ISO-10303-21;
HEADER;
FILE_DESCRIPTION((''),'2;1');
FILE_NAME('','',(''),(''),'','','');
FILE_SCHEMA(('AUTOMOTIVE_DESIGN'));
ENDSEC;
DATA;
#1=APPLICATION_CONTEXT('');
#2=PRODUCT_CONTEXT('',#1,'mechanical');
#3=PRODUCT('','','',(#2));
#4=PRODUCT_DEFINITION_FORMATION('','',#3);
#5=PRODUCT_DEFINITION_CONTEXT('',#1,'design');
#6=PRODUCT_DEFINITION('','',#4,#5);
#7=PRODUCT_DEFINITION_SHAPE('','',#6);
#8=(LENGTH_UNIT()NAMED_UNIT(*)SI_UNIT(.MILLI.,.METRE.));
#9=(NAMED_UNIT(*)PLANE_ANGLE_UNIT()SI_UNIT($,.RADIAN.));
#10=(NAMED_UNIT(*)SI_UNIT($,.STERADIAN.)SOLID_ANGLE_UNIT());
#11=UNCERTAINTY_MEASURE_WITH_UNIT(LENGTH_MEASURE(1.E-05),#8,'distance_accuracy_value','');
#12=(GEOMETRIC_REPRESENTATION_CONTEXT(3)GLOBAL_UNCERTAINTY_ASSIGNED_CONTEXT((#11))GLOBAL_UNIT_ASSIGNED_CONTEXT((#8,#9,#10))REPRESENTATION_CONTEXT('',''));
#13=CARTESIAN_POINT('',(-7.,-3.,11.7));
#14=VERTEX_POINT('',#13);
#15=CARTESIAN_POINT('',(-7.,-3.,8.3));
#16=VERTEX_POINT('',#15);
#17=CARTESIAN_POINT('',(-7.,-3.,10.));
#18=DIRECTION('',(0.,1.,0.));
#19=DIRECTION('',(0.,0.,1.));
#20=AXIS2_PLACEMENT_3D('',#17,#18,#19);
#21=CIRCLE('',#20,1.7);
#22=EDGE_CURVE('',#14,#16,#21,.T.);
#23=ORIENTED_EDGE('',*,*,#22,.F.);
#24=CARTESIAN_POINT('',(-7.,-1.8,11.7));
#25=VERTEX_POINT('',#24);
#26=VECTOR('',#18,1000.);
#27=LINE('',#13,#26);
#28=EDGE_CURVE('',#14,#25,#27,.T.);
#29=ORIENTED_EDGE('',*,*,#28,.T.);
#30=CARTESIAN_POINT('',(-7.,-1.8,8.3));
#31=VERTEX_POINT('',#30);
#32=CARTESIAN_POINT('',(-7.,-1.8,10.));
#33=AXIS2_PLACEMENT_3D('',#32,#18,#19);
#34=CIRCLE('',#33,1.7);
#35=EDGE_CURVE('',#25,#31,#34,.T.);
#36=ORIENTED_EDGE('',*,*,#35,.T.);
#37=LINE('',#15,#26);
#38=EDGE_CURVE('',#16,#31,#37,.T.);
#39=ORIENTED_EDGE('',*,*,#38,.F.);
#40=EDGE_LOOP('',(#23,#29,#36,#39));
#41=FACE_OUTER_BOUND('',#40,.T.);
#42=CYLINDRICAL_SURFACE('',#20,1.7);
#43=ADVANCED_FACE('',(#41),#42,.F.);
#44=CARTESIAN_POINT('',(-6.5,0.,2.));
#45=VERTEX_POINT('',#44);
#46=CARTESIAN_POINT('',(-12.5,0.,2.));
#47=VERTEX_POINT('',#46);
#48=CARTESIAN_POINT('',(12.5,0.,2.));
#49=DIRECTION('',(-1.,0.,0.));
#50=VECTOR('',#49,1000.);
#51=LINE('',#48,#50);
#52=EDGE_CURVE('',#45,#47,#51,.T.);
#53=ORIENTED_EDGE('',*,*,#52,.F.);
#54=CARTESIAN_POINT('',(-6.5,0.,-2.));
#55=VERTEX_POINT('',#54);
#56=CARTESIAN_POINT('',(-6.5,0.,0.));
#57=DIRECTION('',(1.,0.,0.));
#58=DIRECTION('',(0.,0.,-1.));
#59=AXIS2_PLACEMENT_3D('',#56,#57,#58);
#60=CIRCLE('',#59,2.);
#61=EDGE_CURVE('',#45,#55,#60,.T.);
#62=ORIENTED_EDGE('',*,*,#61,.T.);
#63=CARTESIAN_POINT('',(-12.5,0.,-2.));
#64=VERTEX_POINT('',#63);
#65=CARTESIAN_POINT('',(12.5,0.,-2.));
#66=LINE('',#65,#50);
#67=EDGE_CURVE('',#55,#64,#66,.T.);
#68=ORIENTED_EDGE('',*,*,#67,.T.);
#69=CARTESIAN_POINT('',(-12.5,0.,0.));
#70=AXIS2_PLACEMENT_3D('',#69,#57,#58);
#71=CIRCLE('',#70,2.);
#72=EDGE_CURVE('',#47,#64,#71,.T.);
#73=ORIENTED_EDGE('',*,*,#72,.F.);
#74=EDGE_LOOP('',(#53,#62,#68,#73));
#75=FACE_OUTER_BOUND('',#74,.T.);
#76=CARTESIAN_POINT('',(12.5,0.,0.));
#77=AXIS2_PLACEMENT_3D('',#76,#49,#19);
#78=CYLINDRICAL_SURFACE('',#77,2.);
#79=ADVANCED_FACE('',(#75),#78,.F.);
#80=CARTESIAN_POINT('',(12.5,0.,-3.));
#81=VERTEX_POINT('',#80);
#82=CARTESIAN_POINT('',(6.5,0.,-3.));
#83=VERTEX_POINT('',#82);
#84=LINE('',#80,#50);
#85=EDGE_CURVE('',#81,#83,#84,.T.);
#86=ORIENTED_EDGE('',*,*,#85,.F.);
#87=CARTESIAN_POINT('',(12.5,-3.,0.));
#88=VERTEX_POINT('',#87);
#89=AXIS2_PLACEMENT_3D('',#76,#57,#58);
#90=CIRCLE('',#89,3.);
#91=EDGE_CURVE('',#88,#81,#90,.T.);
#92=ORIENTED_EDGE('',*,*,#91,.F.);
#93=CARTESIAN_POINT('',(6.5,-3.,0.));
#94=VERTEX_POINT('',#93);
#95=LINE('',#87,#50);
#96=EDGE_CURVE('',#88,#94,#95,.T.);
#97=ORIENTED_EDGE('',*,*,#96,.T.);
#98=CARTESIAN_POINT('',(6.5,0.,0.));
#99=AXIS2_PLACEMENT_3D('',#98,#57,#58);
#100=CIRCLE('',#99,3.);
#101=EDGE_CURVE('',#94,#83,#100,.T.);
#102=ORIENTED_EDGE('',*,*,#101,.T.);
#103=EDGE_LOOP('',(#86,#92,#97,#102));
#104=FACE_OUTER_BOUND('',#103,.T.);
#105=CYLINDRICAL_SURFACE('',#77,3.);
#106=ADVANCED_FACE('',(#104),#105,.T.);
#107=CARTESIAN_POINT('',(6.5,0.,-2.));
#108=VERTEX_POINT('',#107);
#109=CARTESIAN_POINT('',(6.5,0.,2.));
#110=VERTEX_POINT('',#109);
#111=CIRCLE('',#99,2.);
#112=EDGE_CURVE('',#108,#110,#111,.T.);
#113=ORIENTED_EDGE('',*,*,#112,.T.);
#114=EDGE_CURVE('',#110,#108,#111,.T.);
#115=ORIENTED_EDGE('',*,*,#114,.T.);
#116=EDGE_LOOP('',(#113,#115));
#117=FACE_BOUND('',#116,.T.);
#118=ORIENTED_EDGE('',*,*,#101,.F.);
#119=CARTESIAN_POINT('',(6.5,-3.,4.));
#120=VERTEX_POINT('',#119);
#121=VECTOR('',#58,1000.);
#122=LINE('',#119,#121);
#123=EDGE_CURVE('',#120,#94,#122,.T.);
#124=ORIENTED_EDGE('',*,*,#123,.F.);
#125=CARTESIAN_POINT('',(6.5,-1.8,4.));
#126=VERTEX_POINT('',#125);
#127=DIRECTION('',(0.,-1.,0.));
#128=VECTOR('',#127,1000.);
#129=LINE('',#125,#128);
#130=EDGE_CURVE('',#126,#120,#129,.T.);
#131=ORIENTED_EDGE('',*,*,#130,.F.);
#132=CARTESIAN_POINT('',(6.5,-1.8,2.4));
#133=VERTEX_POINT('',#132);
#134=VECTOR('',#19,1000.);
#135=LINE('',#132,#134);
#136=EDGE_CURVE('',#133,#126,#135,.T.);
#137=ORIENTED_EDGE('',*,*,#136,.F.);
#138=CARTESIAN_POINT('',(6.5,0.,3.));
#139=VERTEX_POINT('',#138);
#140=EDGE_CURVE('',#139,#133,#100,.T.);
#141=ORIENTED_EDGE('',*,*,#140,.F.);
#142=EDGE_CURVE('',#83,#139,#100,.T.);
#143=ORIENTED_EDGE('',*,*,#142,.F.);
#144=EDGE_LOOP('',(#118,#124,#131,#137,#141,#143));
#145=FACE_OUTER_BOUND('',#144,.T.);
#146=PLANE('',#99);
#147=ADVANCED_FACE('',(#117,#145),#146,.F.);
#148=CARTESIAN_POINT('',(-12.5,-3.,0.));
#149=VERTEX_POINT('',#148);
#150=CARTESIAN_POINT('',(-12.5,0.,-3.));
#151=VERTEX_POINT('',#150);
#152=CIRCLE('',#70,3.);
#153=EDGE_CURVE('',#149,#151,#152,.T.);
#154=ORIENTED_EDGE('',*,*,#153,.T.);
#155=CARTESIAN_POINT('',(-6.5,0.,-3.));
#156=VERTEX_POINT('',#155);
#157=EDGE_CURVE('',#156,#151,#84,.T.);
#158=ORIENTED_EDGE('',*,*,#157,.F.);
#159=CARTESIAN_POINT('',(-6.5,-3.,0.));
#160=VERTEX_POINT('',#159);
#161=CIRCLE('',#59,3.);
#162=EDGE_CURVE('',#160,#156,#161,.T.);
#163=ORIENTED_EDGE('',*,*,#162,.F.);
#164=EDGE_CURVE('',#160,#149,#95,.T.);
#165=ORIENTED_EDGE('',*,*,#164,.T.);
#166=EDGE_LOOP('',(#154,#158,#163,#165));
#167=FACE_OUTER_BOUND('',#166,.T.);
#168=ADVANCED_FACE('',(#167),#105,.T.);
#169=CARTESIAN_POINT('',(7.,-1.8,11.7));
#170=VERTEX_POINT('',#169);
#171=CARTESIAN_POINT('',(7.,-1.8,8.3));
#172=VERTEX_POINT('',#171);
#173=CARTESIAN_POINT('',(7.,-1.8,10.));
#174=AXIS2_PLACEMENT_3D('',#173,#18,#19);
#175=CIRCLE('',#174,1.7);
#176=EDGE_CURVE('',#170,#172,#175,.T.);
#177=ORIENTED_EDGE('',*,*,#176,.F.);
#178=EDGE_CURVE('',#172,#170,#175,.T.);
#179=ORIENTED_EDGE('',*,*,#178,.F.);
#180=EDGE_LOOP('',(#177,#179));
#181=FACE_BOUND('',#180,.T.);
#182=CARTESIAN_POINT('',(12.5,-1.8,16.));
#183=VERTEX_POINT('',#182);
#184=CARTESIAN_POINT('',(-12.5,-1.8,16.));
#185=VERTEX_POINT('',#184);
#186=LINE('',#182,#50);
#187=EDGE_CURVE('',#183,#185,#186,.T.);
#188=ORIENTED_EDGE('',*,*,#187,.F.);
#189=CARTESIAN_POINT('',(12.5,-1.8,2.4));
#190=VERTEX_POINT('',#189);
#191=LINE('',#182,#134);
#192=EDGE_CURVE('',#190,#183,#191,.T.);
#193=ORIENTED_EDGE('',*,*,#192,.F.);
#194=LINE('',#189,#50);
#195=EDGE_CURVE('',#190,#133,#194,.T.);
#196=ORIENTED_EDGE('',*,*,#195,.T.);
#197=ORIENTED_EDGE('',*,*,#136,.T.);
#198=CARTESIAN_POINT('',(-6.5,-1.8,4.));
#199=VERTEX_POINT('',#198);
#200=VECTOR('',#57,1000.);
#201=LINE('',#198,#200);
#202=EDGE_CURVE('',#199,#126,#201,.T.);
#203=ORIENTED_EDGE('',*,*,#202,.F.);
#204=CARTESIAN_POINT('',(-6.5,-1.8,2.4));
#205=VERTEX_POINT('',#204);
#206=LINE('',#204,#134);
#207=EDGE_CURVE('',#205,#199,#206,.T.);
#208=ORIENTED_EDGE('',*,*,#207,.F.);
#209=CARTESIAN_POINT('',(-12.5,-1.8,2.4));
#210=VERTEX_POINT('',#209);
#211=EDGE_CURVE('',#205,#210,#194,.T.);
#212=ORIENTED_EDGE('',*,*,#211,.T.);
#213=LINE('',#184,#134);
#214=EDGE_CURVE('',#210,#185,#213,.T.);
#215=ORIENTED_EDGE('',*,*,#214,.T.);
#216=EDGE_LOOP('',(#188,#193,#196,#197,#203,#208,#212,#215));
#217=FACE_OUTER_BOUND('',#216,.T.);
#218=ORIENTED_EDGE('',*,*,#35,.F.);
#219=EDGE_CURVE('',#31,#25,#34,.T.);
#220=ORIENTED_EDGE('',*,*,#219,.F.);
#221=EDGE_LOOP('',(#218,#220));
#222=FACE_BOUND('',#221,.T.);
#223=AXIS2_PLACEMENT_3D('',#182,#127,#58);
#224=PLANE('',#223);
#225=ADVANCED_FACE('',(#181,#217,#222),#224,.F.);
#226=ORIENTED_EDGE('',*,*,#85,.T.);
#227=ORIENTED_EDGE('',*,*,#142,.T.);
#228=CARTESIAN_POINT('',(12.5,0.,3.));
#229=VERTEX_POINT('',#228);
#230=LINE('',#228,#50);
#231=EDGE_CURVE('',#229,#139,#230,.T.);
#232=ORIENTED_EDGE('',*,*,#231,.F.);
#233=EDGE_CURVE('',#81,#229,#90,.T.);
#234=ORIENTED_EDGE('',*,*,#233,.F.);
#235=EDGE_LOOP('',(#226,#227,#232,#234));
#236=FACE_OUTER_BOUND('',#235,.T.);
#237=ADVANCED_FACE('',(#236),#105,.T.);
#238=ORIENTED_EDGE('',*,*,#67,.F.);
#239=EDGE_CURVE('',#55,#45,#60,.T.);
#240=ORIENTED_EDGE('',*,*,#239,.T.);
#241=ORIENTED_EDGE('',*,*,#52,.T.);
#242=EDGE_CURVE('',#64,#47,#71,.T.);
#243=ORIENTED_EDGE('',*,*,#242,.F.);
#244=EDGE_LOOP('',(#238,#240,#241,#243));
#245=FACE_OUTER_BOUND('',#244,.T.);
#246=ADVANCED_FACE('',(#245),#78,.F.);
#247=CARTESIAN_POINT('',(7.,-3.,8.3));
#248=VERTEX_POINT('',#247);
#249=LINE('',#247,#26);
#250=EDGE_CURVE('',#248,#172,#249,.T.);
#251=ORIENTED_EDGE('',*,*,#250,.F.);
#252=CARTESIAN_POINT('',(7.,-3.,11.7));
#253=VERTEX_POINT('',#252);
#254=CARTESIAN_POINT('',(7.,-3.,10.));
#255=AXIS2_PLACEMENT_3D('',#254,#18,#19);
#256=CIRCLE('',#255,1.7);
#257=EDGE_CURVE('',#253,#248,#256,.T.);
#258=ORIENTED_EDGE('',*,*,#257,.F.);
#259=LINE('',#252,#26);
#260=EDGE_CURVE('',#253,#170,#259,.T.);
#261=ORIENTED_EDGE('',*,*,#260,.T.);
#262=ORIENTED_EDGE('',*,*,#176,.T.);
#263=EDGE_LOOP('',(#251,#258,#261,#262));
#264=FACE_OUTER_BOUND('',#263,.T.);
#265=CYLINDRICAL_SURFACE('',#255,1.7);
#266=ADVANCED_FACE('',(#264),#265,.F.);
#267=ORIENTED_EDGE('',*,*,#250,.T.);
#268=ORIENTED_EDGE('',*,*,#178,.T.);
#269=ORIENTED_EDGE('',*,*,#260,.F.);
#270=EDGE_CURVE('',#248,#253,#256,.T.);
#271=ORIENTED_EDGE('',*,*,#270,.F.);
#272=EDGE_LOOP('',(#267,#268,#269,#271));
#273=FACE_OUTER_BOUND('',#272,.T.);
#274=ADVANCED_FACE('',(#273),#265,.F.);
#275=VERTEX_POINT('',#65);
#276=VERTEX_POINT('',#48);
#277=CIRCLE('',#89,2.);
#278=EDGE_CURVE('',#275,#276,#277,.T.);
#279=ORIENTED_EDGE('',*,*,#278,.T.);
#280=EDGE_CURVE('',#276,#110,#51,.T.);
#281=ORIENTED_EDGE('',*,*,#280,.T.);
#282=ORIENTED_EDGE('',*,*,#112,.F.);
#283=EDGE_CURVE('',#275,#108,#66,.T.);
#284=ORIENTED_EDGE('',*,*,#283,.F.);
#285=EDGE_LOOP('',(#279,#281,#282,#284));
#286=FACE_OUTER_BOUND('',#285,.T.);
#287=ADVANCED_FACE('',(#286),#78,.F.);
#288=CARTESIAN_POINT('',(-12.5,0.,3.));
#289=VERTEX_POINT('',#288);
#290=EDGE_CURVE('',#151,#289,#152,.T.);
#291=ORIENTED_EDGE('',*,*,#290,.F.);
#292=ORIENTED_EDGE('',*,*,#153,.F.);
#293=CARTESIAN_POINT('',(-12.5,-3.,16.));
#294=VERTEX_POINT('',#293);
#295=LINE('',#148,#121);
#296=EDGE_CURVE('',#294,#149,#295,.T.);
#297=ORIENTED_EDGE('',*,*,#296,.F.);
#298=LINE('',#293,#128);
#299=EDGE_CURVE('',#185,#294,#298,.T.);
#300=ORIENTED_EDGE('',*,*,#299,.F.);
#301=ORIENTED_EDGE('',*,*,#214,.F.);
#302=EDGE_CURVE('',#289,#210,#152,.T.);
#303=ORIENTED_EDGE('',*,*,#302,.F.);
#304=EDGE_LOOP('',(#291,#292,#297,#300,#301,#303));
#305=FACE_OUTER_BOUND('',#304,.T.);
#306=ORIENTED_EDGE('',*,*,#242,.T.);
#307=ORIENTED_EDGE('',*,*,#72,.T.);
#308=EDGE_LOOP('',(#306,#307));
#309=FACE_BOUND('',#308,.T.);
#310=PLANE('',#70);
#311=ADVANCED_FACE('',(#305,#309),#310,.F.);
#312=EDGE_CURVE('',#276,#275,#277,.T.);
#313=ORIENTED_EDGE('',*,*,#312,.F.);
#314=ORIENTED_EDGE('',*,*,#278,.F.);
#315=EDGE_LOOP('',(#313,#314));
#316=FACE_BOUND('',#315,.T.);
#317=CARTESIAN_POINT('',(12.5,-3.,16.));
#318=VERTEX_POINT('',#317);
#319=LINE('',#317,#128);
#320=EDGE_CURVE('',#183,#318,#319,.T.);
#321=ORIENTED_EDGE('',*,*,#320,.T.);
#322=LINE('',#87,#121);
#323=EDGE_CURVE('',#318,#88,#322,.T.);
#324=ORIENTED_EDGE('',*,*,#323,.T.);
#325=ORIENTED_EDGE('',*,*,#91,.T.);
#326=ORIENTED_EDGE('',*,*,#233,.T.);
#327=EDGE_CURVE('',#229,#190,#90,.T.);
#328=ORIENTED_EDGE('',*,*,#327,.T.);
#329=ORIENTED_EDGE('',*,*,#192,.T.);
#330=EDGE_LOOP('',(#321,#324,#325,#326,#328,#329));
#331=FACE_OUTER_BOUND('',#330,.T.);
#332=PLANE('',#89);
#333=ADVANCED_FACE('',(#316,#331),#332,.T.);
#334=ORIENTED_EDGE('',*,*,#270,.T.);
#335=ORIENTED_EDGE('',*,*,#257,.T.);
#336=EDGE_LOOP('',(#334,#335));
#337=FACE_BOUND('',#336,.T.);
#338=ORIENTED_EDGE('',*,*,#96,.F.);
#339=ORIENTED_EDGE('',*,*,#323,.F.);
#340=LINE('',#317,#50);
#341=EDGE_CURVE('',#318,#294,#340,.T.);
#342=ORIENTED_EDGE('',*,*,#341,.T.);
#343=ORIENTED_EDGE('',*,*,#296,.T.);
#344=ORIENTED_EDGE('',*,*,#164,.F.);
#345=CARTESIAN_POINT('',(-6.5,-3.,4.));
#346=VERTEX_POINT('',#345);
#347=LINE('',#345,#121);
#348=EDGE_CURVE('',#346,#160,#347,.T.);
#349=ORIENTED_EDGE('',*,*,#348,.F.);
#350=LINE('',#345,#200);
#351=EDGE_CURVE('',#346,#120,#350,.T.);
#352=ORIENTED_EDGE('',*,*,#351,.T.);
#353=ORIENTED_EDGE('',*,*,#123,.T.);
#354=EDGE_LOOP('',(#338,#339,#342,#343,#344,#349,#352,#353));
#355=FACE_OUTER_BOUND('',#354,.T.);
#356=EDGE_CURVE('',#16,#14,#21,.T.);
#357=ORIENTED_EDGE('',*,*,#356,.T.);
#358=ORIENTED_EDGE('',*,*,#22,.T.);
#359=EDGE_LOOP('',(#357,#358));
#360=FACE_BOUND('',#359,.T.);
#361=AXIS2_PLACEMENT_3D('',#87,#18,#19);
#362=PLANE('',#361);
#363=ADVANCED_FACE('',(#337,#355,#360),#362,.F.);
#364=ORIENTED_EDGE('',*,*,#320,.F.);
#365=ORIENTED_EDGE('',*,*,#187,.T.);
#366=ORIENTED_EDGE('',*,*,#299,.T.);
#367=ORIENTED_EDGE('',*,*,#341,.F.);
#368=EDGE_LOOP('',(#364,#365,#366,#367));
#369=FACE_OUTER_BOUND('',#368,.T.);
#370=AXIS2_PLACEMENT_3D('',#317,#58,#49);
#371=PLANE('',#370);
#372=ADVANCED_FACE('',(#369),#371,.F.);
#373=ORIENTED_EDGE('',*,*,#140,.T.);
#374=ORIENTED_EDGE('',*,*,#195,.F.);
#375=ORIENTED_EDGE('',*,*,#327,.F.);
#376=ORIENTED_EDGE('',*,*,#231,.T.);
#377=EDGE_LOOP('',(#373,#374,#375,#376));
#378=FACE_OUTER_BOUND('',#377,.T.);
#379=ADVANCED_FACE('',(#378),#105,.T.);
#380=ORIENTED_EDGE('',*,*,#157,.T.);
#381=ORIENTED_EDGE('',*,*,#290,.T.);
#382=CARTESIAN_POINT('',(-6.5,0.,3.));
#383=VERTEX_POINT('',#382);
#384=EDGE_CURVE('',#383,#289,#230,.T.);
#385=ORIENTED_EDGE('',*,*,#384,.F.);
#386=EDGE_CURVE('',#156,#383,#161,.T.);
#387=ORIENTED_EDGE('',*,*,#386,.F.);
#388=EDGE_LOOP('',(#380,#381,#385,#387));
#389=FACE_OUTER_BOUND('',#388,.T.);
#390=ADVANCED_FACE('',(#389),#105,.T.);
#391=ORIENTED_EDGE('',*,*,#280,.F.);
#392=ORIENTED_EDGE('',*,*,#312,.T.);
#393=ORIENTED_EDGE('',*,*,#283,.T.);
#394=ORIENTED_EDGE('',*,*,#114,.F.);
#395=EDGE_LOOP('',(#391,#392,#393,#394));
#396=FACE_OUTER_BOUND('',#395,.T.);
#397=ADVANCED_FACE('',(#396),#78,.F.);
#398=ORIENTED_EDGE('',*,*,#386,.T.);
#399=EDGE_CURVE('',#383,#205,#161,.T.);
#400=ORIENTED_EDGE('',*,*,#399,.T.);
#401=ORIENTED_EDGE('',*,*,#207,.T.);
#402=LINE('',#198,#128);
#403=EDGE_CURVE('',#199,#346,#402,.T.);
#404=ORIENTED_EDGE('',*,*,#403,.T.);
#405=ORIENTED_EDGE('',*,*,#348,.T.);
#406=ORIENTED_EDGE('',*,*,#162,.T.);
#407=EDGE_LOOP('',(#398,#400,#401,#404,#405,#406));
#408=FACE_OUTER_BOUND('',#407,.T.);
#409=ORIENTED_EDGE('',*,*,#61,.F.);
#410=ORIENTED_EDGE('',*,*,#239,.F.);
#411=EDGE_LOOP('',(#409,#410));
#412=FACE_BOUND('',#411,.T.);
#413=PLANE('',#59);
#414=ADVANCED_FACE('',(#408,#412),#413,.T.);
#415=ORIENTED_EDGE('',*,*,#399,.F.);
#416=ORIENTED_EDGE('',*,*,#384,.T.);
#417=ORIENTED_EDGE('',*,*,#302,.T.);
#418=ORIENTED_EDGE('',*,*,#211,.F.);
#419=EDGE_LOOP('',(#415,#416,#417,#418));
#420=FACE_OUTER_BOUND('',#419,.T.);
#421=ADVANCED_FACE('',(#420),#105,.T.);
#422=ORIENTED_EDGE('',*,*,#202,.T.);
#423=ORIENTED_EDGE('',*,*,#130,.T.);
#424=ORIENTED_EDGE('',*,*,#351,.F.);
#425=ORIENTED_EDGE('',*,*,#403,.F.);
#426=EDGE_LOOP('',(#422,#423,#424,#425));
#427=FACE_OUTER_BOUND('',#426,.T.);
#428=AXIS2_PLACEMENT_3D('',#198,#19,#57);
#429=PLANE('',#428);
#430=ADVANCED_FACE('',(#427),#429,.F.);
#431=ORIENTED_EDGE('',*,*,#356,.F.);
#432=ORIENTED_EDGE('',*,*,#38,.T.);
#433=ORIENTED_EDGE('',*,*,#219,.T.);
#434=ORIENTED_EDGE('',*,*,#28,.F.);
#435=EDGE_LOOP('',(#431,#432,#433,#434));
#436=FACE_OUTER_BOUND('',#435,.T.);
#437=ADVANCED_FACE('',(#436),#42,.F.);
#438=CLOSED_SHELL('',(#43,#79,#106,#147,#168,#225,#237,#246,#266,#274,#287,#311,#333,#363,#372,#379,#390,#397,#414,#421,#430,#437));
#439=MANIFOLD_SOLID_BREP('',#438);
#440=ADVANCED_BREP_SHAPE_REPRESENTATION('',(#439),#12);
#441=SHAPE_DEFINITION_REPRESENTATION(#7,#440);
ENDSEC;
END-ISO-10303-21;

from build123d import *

# Parameters (mm, degrees)
SKETCH_1_R          = 2
EXTRUDE_1_DEPTH     = 12.5
SKETCH_2_R          = 1.7
CUT_EXTRUDE_1_DEPTH = 21.863604674
CUT_EXTRUDE_2_DEPTH = 6.5


with BuildPart() as part:
    # 草图1 → 凸台-拉伸1 (new, symmetric)
    with BuildSketch(Plane(origin=(0, 0, 0), x_dir=(0, 0, -1), z_dir=(1, 0, 0))):
        with BuildLine():
            Line((0, -3), (-16, -3))
            Line((-16, -3), (-16, -1.8))
            Line((-16, -1.8), (-2.4, -1.8))
            ThreePointArc((-2.4, -1.8), (1.341640786, 2.683281573), (0, -3))
        make_face()
        Circle(SKETCH_1_R, mode=Mode.SUBTRACT)
    extrude(amount=EXTRUDE_1_DEPTH, both=True)

    # 草图2 → 切除-拉伸1 (cut, through all)
    with BuildSketch(Plane(origin=(0, -1.8, 0), x_dir=(1, 0, 0), z_dir=(0, 1, 0))):
        with Locations(Location((-7, -10, 0), (0, 0, 270))):
            Circle(SKETCH_2_R)
        with Locations(Location((7, -10, 0), (0, 0, 270))):
            Circle(SKETCH_2_R)
    extrude(amount=-CUT_EXTRUDE_1_DEPTH, mode=Mode.SUBTRACT)

    # 草图3 → 切除-拉伸2 (cut, symmetric)
    with BuildSketch(Plane(origin=(0, 0, 0), x_dir=(0, 0, -1), z_dir=(1, 0, 0))):
        with BuildLine():
            Line((-4, -3), (0, -3))
            ThreePointArc((0, -3), (1.341640786, 2.683281573), (-2.4, -1.8))
            Line((-2.4, -1.8), (-4, -1.8))
            Line((-4, -1.8), (-4, -3))
        make_face()
    extrude(amount=CUT_EXTRUDE_2_DEPTH, both=True, mode=Mode.SUBTRACT)


solid = part.part
